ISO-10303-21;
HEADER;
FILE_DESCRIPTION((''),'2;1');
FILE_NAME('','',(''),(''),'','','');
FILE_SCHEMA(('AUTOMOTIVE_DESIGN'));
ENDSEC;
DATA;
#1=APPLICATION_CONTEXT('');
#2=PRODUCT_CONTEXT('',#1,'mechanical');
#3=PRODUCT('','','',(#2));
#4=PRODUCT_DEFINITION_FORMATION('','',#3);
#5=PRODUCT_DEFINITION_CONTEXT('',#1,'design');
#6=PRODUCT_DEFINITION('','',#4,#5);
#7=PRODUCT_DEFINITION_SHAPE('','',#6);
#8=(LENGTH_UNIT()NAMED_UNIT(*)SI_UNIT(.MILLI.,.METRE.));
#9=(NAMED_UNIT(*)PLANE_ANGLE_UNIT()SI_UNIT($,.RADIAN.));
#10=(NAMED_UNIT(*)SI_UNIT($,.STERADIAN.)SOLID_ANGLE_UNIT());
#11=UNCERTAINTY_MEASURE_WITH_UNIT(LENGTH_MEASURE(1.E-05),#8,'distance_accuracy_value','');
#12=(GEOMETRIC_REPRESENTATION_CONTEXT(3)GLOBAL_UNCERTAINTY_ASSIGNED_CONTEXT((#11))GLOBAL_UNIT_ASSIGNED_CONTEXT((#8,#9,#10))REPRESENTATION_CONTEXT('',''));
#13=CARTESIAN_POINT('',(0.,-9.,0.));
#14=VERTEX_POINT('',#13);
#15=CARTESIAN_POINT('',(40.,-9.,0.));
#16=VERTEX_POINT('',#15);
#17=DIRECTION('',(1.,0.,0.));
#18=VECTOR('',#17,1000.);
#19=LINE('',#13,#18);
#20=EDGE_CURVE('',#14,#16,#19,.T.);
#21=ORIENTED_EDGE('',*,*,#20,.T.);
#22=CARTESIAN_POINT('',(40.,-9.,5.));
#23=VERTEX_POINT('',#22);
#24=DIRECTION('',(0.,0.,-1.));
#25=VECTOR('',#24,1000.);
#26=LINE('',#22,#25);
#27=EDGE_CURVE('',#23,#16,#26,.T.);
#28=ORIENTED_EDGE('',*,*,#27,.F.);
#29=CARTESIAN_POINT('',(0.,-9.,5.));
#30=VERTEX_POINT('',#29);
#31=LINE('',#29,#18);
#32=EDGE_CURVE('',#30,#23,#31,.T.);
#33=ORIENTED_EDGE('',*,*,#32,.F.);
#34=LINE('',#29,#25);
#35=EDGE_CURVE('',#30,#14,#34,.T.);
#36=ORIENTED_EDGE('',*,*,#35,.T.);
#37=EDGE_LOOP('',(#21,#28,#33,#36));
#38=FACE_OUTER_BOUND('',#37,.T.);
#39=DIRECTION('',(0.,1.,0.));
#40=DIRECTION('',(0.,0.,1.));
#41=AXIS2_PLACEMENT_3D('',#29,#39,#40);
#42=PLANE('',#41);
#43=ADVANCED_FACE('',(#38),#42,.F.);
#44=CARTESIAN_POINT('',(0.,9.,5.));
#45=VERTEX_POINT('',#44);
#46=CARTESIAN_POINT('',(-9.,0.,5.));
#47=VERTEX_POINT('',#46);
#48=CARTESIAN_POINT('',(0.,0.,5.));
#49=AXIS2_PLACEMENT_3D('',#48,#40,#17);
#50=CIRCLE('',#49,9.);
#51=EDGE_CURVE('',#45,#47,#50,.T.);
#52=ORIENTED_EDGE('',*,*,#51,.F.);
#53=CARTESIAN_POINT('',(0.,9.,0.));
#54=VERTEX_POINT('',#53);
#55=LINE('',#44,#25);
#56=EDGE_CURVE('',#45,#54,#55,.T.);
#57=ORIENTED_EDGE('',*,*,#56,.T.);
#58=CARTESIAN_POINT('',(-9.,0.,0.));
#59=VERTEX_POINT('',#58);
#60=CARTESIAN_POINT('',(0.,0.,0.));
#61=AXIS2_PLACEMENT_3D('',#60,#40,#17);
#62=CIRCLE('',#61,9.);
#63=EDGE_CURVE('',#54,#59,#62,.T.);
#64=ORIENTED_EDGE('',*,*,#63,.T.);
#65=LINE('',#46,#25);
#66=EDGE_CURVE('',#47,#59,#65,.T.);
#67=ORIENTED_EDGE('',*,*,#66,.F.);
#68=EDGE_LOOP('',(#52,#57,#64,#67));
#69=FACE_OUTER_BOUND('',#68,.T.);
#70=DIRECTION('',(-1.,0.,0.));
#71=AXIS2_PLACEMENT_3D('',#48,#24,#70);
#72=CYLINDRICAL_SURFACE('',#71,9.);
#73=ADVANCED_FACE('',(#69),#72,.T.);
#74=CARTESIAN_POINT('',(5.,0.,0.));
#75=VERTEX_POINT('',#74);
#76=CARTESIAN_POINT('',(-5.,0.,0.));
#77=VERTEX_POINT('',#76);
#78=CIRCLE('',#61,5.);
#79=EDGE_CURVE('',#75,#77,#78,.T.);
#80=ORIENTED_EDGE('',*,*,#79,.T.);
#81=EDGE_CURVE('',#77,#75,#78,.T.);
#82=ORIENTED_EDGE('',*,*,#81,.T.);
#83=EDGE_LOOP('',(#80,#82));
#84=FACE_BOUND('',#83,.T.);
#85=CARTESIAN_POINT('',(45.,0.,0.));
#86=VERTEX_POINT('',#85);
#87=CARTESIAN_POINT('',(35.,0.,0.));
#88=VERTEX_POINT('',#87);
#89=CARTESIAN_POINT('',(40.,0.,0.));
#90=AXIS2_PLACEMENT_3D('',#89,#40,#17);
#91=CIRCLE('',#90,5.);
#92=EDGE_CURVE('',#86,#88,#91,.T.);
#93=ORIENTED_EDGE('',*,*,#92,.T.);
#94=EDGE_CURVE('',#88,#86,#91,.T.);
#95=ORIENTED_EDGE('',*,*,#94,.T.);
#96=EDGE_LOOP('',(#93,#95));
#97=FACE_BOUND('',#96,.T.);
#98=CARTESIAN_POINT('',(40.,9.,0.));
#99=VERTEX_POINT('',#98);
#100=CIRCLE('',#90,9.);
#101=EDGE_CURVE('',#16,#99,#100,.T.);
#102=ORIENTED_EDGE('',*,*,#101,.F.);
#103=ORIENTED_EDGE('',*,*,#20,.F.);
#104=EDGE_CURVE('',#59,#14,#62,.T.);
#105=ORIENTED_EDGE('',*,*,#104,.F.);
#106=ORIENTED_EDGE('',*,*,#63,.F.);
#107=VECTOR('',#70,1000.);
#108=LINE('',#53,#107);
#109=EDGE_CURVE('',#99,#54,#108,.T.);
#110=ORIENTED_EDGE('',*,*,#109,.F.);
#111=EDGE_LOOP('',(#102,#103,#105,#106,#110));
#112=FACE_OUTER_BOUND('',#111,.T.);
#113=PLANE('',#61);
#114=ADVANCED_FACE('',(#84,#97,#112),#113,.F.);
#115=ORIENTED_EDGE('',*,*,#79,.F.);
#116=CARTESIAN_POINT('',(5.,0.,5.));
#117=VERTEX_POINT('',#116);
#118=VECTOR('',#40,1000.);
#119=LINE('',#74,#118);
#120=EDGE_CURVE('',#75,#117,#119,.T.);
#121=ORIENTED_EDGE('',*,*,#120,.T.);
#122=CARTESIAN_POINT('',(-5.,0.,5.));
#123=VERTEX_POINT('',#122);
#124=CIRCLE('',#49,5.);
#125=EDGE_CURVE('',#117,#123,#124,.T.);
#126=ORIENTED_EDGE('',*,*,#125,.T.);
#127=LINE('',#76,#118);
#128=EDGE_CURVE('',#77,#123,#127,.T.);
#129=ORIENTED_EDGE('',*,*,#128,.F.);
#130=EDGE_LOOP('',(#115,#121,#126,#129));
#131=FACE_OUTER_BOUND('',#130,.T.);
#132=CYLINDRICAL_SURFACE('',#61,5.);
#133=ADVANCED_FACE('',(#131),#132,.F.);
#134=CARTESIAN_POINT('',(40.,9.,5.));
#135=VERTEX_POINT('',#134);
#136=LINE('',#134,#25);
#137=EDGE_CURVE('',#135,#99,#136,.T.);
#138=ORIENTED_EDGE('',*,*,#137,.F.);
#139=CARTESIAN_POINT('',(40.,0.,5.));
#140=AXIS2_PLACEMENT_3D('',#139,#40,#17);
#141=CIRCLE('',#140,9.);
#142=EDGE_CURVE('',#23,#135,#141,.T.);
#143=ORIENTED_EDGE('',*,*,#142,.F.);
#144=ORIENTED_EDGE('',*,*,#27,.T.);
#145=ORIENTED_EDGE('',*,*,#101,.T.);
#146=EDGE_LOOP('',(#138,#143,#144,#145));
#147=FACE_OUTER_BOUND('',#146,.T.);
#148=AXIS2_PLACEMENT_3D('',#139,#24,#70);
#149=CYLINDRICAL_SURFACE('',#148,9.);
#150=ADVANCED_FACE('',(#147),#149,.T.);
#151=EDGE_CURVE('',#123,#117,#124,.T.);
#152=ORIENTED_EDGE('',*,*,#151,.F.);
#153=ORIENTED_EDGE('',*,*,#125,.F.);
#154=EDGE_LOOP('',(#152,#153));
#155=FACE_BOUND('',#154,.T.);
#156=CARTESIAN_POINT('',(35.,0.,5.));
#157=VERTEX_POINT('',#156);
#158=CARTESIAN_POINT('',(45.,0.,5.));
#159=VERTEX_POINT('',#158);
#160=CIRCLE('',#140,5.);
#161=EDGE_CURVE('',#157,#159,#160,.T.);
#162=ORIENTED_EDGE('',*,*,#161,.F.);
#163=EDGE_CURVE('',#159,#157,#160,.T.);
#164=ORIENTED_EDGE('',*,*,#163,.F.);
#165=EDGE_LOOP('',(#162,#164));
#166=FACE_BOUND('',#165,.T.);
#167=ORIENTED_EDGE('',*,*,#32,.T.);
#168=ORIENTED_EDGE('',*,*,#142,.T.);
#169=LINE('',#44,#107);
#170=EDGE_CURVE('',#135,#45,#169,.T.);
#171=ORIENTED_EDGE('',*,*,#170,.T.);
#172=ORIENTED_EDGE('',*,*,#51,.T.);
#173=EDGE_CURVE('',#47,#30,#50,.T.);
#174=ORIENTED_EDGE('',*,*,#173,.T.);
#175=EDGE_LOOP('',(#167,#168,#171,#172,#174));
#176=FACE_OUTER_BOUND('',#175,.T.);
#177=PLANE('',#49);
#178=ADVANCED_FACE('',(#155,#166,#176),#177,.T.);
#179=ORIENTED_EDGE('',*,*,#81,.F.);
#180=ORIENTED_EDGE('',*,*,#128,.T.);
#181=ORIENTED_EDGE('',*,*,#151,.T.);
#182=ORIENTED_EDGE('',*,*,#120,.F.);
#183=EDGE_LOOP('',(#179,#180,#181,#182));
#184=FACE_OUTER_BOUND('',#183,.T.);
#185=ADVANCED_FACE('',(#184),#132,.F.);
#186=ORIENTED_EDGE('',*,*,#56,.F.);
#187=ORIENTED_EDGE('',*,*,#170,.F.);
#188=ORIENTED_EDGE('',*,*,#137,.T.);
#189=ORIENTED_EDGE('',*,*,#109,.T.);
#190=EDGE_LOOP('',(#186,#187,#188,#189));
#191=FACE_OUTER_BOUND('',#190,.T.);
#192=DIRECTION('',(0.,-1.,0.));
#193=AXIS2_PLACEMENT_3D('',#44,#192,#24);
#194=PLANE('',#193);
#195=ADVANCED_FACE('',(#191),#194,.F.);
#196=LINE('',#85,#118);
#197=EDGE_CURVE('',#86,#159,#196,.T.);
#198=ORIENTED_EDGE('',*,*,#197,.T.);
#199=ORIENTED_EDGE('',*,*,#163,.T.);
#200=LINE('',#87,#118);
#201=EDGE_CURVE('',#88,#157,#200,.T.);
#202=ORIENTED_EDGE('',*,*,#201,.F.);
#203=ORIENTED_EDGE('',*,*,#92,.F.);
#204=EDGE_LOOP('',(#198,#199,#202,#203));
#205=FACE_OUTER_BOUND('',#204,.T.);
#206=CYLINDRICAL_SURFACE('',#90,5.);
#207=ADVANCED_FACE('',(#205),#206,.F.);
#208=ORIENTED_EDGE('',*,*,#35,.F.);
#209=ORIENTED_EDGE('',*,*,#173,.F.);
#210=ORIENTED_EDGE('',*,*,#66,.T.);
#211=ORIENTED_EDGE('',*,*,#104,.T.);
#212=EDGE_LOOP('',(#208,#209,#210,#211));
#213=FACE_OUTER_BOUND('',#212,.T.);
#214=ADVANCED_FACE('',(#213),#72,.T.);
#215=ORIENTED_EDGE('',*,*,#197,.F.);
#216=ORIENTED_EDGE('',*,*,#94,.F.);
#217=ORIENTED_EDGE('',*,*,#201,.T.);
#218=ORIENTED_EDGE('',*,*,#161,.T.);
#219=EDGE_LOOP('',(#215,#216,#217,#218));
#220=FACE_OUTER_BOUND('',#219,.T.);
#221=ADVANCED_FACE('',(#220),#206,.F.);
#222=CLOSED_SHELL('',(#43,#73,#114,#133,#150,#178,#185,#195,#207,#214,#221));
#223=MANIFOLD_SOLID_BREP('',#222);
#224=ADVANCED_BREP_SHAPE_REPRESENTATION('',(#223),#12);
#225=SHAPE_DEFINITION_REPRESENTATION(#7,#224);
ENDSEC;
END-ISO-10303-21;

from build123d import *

# Parameters (mm, degrees)
BASE_EXTRUDE_DEPTH = 5
SKETCH2_R          = 5
CUT_EXTRUDE1_DEPTH = 51.069951068


with BuildPart() as part:
    # Sketch1 → Base-Extrude (new body)
    with BuildSketch(Plane.XY):
        with BuildLine():
            Line((0, 9), (40, 9))
            ThreePointArc((40, 9), (49, 0), (40, -9))
            Line((40, -9), (0, -9))
            ThreePointArc((0, -9), (-9, 0), (0, 9))
        make_face()
    extrude(amount=BASE_EXTRUDE_DEPTH)

    # Sketch2 → Cut-Extrude1 (cut, through all)
    with BuildSketch(Plane.XY.offset(5)):
        Circle(SKETCH2_R)
        with Locations((40, 0)):
            Circle(SKETCH2_R)
    extrude(amount=-CUT_EXTRUDE1_DEPTH, mode=Mode.SUBTRACT)


solid = part.part
